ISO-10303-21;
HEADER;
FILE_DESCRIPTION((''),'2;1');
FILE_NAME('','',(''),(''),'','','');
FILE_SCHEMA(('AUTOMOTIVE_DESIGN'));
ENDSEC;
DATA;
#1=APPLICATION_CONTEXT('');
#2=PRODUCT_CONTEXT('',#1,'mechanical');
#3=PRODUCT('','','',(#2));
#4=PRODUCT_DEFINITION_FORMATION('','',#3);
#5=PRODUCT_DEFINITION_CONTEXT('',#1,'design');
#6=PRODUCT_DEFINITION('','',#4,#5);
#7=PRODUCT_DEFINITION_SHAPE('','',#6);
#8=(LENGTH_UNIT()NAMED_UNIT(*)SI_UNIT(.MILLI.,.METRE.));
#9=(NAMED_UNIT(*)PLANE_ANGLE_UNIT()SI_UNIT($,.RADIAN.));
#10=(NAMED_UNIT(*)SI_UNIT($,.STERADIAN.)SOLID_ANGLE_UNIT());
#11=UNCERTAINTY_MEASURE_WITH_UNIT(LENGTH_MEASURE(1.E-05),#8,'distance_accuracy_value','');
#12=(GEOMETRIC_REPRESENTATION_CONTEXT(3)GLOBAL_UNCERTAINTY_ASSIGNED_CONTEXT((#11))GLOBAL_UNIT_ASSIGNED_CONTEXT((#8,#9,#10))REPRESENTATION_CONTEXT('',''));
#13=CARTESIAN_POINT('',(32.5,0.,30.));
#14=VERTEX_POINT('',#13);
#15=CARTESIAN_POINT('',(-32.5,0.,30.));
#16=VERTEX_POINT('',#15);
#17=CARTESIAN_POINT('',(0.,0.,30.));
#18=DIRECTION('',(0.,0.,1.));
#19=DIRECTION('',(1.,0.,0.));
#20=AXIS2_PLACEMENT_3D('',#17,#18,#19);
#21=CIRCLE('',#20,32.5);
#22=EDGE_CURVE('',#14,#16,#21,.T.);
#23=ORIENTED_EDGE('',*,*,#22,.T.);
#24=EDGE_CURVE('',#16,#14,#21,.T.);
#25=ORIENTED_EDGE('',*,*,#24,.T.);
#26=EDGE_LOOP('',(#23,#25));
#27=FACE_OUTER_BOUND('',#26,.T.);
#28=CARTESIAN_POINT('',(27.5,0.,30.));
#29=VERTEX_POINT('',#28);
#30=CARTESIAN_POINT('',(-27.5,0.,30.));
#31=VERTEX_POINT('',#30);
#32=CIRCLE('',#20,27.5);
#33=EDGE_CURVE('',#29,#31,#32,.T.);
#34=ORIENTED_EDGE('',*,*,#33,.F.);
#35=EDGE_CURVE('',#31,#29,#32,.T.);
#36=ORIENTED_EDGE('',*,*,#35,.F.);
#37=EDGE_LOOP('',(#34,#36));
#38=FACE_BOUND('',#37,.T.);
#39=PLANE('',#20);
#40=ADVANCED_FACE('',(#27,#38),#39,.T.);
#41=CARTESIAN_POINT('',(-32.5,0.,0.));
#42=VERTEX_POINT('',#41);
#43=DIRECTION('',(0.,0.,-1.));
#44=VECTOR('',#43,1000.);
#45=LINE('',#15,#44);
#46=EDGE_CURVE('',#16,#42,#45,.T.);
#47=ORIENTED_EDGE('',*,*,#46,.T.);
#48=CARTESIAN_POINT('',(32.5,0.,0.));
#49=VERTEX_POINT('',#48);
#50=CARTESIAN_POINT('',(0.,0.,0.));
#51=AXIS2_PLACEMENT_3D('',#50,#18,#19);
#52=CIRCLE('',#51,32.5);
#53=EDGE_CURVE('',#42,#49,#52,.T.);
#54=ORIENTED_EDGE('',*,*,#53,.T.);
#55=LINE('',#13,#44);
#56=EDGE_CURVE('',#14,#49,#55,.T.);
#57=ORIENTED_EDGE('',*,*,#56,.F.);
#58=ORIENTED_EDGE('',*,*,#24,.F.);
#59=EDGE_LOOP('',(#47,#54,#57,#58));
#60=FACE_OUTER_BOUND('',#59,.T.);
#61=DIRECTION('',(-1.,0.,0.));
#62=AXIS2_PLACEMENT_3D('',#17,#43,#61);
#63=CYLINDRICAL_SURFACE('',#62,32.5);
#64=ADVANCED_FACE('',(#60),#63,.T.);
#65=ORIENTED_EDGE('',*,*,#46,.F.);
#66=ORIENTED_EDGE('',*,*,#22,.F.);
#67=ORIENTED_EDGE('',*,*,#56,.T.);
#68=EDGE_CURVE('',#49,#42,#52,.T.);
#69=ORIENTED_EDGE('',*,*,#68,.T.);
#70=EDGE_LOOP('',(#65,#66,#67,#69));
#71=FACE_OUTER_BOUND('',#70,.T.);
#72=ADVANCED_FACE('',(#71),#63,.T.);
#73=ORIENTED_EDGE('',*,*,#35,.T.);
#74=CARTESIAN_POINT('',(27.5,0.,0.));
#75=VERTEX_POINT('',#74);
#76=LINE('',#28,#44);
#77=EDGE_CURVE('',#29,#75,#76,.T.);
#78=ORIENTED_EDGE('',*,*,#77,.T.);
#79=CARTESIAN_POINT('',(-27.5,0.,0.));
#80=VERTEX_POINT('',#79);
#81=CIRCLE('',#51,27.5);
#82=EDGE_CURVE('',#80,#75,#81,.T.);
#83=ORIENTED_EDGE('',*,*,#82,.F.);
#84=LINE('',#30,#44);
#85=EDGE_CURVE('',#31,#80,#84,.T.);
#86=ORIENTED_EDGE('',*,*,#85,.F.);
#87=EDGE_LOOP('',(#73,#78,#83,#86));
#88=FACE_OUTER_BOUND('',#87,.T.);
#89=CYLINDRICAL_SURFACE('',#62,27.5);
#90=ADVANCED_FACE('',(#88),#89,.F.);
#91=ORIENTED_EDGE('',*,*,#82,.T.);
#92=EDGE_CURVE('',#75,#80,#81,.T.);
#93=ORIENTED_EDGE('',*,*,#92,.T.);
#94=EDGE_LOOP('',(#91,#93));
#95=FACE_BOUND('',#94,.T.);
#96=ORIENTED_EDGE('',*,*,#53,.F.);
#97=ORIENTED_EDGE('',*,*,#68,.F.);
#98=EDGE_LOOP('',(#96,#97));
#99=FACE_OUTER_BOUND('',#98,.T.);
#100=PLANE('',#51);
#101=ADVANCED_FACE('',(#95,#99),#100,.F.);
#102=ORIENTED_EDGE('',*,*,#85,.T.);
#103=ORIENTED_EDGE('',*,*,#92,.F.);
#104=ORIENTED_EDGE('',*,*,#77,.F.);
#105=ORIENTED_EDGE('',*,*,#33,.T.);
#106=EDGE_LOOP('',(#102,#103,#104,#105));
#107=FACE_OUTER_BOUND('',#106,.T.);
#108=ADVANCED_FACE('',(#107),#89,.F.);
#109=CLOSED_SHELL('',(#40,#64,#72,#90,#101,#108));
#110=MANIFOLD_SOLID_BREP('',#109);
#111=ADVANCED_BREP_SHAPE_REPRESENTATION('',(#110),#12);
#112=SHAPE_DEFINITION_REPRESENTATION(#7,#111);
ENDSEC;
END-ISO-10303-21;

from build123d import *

# Parameters (mm, degrees)
SKETCH1_R           = 32.5
SKETCH1_R_2         = 27.5
BOSS_EXTRUDE1_DEPTH = 30


with BuildPart() as part:
    # Sketch1 → Boss-Extrude1 (new body)
    with BuildSketch(Plane.XY):
        Circle(SKETCH1_R)
        Circle(SKETCH1_R_2, mode=Mode.SUBTRACT)
    extrude(amount=BOSS_EXTRUDE1_DEPTH)


solid = part.part
